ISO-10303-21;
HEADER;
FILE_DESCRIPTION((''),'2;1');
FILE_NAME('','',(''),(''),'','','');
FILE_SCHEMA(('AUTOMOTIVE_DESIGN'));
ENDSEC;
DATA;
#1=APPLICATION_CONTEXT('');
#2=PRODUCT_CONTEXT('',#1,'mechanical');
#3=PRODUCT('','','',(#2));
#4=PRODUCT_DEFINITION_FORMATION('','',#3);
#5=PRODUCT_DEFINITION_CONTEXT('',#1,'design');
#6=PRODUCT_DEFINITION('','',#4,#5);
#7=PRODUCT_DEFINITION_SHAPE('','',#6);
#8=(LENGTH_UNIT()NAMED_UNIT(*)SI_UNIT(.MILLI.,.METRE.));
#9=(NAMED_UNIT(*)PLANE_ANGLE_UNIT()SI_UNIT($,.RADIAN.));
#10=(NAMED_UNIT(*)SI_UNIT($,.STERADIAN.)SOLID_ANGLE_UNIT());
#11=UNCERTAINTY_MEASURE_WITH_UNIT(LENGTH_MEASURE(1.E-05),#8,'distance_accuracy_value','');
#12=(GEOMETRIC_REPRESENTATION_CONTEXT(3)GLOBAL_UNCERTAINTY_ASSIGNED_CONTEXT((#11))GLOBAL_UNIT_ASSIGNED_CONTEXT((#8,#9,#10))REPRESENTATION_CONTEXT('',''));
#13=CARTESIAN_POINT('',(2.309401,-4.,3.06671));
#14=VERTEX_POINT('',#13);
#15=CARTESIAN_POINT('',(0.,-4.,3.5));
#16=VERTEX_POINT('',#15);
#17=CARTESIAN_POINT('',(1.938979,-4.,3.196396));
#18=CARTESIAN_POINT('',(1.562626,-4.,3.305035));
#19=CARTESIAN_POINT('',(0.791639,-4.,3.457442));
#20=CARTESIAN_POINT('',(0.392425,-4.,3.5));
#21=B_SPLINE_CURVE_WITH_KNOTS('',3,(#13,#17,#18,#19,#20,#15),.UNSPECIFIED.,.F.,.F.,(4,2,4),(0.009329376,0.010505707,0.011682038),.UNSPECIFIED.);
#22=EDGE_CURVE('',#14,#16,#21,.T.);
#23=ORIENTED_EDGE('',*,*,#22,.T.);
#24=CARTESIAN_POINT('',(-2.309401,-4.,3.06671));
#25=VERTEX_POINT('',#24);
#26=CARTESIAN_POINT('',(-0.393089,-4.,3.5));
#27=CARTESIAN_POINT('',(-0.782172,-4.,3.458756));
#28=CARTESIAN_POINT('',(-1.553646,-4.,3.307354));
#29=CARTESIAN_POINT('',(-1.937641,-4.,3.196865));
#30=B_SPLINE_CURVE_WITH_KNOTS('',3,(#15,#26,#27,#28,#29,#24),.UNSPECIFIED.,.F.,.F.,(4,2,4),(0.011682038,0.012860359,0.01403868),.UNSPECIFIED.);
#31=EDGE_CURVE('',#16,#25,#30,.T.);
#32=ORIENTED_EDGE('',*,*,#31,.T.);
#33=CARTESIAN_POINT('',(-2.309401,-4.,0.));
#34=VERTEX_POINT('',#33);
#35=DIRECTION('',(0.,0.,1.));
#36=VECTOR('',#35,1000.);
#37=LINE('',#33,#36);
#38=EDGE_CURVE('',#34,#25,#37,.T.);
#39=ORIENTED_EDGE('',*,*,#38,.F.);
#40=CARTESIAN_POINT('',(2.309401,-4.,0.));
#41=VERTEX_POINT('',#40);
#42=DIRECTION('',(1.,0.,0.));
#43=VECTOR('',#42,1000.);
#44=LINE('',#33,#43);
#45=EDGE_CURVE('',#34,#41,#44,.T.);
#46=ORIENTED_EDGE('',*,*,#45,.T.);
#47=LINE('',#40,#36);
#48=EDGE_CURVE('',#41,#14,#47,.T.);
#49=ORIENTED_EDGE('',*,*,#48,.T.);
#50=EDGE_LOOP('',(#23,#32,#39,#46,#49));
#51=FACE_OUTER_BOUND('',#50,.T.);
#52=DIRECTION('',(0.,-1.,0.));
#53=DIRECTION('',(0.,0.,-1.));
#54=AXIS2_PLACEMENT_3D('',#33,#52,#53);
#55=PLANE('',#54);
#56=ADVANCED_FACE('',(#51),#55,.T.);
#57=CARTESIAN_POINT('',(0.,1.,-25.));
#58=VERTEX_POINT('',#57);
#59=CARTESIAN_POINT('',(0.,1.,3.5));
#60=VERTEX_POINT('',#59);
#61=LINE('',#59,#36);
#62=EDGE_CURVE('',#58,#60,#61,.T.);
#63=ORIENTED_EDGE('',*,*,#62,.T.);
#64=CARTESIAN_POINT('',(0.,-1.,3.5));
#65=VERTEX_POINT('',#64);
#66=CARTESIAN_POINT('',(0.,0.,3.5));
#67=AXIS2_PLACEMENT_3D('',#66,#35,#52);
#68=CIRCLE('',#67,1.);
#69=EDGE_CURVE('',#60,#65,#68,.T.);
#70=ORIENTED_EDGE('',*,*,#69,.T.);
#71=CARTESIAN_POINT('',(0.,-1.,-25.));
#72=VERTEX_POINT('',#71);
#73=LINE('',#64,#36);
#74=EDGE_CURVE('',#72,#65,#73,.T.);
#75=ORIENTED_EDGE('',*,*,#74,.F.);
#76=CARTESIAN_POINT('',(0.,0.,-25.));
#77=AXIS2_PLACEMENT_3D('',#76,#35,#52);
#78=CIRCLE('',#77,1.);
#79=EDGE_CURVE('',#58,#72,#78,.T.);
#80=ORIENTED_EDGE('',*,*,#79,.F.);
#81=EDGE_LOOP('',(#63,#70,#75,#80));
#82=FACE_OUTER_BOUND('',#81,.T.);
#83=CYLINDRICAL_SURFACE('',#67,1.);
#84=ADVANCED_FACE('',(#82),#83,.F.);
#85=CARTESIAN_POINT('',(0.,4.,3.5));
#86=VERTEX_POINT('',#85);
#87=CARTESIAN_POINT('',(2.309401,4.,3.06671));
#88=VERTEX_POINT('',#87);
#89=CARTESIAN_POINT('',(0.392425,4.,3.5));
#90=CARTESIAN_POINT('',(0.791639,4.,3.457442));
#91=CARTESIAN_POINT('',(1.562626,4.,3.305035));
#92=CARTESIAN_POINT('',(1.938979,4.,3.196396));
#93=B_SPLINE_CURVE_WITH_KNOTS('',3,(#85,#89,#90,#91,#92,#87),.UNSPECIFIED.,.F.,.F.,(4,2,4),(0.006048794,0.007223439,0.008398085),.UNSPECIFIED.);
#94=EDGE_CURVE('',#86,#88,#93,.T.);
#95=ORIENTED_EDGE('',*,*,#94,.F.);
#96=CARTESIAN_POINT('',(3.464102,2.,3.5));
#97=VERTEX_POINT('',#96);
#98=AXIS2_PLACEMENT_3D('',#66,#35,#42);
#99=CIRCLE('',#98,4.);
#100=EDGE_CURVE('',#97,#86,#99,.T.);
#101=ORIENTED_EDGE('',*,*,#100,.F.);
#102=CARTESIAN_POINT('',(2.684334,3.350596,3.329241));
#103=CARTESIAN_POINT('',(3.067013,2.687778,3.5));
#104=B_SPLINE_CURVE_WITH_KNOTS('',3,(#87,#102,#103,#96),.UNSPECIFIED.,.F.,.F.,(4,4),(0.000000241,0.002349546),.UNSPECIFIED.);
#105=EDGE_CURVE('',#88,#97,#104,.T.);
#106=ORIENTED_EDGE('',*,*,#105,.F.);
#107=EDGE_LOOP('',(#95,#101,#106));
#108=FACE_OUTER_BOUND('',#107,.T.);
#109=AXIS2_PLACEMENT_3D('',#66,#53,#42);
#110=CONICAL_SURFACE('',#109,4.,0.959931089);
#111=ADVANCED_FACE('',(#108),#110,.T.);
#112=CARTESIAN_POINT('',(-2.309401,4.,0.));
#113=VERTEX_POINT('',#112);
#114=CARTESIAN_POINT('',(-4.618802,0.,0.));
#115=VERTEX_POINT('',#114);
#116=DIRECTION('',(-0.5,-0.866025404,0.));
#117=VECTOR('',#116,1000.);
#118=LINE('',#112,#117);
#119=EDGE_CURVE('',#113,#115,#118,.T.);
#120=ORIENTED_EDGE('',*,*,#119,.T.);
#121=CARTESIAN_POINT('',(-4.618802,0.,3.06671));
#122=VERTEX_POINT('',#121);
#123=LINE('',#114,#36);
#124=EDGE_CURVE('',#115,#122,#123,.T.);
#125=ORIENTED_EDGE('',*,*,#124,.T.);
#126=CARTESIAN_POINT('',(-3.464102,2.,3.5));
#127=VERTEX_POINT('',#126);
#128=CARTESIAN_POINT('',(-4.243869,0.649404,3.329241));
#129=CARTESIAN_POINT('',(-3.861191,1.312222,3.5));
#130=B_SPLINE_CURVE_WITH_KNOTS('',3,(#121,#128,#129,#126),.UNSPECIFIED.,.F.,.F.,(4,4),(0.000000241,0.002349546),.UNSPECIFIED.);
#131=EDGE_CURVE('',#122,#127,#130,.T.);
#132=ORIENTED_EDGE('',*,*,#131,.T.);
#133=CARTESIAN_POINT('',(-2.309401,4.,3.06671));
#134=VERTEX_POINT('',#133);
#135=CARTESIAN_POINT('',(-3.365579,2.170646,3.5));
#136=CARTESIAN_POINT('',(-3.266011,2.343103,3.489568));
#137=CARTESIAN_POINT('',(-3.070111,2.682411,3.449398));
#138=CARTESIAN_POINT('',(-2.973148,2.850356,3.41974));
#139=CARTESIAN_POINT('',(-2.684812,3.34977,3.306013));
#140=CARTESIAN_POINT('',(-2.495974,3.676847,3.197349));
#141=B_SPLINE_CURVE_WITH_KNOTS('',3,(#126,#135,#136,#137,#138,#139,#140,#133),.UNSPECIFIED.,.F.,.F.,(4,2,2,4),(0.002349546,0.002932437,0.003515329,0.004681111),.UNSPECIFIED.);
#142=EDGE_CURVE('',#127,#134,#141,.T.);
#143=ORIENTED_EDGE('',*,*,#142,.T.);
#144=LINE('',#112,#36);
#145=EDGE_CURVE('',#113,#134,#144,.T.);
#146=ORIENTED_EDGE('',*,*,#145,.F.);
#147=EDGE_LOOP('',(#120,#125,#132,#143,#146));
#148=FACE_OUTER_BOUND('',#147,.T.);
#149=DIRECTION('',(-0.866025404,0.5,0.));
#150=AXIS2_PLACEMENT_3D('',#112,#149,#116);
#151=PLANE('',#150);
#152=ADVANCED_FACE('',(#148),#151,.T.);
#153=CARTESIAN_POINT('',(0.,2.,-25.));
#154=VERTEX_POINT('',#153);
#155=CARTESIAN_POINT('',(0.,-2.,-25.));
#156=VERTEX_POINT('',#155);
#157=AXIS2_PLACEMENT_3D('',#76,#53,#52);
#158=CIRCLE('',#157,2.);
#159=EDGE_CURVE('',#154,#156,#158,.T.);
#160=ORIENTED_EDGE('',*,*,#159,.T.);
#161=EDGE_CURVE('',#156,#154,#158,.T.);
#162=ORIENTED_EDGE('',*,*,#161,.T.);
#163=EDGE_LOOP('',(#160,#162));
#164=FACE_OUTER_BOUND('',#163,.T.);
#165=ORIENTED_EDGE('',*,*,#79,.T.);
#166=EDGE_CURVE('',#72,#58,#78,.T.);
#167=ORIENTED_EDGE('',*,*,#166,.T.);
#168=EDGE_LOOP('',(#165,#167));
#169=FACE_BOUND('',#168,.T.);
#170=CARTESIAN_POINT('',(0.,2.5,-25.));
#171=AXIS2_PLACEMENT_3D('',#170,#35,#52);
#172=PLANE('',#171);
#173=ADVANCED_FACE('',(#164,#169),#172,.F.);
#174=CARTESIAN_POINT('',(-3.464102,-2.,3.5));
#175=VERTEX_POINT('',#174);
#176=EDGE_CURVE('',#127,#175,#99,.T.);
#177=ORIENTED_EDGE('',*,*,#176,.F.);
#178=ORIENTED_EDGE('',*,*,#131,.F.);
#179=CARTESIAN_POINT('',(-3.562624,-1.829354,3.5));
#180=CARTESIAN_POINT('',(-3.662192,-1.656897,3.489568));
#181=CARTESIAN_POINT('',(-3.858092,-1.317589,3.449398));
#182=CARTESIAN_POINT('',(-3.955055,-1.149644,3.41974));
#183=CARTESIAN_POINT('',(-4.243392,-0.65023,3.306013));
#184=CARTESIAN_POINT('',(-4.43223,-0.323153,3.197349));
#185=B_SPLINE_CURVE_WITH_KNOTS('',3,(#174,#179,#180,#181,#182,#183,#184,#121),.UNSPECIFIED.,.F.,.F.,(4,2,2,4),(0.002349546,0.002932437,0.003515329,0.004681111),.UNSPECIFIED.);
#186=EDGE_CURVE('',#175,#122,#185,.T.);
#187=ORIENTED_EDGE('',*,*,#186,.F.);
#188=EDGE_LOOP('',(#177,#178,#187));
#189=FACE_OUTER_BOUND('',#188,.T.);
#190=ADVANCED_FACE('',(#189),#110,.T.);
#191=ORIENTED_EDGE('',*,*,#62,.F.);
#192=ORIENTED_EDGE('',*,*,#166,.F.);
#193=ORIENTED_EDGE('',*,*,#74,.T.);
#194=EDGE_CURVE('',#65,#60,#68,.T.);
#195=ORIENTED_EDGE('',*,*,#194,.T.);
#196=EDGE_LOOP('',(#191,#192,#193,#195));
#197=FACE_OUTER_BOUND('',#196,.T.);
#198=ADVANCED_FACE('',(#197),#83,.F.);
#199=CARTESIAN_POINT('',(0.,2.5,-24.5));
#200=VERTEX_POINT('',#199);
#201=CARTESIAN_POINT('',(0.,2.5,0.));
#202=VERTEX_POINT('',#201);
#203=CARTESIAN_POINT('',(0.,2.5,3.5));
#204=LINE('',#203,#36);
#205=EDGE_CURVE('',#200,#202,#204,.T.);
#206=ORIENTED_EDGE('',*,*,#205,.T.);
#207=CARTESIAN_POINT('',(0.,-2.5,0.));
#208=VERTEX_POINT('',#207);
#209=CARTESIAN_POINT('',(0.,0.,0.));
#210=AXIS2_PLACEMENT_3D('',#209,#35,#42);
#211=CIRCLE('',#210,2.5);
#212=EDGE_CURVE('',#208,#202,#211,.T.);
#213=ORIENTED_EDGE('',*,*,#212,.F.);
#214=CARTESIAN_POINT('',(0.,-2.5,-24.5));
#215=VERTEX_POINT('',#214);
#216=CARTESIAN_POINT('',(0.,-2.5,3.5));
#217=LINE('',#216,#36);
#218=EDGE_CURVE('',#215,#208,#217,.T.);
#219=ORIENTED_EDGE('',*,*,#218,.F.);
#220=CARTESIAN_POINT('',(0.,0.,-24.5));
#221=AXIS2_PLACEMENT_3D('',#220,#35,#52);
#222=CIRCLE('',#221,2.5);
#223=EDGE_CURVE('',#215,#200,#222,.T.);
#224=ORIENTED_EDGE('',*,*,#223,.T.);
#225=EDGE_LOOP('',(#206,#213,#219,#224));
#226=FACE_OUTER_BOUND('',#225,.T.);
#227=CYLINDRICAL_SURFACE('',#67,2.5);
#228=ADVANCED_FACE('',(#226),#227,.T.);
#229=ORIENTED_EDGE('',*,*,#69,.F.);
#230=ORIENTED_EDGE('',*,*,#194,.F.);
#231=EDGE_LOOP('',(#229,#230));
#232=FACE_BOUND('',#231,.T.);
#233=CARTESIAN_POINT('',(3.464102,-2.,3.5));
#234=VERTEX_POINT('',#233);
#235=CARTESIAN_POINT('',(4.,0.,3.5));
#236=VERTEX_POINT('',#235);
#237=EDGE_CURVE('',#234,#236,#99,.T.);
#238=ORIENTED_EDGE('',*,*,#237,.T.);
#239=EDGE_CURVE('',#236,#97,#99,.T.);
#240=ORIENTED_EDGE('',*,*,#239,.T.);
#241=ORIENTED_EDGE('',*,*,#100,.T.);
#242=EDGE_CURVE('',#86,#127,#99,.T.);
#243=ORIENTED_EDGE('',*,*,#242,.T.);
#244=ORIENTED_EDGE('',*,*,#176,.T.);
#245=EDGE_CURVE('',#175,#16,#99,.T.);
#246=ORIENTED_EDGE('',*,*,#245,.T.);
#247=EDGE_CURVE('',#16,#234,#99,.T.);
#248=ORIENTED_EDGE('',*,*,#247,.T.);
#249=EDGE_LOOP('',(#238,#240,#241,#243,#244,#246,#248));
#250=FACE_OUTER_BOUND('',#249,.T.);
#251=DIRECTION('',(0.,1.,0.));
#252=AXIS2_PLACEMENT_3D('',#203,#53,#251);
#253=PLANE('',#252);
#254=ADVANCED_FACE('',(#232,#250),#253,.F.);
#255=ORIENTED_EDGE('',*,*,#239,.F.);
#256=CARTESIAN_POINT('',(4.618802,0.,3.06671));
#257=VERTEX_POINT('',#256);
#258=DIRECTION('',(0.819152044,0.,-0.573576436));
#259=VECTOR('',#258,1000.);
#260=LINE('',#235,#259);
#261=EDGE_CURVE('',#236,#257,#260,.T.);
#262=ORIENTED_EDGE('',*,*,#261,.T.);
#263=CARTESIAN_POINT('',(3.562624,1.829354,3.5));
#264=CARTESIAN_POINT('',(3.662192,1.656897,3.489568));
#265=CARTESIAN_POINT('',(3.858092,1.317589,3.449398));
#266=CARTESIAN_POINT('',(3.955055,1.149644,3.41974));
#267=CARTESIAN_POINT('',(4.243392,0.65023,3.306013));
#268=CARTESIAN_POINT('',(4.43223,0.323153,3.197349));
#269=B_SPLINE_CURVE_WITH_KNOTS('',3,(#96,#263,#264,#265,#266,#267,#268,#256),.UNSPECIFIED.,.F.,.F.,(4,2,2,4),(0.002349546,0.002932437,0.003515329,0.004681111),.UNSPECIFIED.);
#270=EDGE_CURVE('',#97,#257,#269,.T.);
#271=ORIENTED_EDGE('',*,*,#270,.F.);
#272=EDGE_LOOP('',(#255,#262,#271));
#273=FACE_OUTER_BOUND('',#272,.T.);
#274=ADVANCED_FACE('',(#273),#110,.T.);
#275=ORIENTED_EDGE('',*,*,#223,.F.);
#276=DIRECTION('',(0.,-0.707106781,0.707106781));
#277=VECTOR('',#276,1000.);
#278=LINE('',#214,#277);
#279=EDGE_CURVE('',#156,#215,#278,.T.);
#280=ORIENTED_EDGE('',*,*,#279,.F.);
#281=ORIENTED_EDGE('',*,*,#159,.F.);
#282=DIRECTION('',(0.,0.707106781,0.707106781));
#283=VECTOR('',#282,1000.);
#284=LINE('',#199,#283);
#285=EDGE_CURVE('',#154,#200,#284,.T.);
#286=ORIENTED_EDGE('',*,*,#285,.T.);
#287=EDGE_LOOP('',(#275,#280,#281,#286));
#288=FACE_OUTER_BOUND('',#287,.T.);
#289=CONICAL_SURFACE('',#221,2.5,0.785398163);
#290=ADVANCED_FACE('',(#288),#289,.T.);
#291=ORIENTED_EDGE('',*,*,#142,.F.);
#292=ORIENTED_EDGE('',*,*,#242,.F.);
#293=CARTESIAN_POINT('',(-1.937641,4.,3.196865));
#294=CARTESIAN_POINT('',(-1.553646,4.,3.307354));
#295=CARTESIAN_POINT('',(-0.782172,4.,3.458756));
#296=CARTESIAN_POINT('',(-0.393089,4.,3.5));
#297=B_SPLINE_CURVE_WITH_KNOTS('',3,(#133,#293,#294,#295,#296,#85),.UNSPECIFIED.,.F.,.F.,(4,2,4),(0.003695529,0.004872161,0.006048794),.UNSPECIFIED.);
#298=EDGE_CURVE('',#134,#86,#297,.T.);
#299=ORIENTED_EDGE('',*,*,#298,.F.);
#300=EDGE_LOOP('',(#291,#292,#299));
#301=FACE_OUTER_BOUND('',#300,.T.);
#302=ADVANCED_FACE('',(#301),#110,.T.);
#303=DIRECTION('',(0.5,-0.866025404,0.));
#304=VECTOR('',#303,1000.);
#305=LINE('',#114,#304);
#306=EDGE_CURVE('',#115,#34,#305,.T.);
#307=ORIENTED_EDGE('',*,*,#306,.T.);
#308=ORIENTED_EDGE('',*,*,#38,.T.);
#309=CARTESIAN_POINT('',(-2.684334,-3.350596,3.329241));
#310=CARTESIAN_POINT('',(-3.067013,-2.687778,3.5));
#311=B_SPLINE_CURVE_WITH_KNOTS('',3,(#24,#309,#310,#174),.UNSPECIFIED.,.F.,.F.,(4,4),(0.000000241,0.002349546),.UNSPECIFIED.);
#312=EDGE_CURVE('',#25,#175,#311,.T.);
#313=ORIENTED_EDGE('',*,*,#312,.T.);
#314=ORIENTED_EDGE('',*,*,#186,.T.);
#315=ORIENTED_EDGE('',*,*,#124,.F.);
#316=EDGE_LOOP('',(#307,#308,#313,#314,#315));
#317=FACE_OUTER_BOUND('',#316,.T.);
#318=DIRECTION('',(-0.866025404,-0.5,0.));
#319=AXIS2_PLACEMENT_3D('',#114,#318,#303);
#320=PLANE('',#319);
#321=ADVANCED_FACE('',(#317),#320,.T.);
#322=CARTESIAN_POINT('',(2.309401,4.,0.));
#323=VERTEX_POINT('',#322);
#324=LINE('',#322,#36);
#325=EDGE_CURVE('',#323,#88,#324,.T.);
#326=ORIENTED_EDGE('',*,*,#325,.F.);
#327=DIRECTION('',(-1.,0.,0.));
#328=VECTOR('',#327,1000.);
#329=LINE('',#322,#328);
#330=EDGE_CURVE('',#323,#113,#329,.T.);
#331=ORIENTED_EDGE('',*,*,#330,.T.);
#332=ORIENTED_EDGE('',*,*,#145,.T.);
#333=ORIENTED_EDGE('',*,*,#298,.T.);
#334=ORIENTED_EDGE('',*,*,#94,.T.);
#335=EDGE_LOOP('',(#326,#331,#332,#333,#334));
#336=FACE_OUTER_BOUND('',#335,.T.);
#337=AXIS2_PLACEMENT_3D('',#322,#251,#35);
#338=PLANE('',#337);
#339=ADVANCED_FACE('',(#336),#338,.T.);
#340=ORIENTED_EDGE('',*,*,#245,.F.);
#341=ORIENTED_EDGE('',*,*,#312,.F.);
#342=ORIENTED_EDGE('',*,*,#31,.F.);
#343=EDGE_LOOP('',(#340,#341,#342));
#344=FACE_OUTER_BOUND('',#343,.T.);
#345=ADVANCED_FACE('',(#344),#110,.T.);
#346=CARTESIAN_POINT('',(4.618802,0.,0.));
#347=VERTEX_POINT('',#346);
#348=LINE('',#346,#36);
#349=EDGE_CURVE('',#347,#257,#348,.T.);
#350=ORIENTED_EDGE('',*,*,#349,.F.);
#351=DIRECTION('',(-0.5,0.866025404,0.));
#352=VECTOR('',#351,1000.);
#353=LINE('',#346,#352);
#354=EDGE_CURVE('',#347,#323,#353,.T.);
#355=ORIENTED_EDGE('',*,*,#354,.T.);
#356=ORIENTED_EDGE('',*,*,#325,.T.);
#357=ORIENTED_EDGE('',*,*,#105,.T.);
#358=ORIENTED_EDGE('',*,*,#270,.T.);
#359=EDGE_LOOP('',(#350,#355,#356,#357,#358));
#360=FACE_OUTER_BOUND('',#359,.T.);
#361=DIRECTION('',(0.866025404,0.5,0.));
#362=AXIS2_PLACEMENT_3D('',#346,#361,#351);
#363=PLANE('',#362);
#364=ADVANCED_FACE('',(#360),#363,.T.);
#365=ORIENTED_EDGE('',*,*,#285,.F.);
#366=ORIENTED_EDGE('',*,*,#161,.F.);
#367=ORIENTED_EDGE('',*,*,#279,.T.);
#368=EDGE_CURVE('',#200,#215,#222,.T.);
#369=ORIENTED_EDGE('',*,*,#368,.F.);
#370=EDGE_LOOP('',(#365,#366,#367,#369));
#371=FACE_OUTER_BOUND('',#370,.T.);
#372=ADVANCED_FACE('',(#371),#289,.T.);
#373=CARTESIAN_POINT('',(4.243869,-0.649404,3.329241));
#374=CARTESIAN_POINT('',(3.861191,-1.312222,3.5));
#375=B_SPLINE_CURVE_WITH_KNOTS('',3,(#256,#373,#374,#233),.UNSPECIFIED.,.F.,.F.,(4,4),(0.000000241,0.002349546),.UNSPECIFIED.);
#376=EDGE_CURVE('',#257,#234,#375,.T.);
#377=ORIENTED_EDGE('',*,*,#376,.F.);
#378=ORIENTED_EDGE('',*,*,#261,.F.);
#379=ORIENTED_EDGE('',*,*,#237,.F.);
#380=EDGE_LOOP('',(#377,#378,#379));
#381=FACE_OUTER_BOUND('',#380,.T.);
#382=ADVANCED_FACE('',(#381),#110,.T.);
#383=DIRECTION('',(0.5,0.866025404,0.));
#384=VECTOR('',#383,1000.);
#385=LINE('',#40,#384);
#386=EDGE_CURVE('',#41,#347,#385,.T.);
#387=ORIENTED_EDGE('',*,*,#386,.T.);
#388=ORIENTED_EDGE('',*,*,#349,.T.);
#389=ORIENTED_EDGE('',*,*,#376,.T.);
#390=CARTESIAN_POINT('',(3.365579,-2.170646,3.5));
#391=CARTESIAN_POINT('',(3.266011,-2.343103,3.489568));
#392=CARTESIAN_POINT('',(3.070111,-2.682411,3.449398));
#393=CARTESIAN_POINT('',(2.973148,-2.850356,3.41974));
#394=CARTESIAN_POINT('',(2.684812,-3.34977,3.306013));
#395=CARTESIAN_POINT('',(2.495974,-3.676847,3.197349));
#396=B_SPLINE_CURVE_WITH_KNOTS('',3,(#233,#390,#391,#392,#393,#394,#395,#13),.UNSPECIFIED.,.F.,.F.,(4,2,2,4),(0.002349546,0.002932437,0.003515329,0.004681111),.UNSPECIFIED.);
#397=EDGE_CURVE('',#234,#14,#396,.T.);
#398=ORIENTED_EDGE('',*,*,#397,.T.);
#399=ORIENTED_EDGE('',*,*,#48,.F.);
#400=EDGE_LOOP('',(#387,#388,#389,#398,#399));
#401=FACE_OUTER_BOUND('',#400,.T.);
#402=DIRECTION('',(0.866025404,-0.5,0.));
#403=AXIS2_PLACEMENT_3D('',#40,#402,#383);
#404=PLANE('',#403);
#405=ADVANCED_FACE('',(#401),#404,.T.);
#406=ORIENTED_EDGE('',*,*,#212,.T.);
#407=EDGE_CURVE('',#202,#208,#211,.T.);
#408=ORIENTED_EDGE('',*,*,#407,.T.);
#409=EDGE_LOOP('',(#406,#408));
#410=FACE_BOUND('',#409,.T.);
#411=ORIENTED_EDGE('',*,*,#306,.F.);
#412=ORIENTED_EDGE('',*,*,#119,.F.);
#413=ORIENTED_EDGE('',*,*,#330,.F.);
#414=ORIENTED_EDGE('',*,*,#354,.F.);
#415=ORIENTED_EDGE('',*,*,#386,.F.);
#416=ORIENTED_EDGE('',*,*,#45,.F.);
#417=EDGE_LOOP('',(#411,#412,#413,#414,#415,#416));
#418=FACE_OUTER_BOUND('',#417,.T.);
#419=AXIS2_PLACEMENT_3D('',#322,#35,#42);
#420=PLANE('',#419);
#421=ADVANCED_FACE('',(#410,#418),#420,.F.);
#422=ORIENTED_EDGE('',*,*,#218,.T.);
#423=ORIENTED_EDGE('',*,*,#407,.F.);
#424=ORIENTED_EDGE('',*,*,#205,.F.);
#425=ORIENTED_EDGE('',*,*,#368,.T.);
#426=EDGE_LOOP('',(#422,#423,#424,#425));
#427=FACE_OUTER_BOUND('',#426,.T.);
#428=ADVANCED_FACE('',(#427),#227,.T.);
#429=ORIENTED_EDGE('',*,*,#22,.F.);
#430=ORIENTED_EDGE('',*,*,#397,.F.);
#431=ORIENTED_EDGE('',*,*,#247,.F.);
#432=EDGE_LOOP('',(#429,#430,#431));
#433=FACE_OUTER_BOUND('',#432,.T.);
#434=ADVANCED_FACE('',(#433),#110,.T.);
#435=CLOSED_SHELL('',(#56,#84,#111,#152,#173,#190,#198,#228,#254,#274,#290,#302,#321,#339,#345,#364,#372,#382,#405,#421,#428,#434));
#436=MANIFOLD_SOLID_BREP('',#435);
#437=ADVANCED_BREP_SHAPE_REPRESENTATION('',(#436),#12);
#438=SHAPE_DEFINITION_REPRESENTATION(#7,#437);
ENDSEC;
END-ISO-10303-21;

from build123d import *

# Parameters (mm, degrees)
BOSS_EXTRUDE1_START = -3.5
SKETCH4_R           = 1
BOSS_EXTRUDE1_DEPTH = 3.5
SKETCH5_R           = 5.237604307
SKETCH5_R_2         = 4
CUT_EXTRUDE1_DEPTH  = 1
CUT_EXTRUDE1_DRAFT  = -55
CHAMFER1_SIZE       = 0.5


with BuildPart() as part:
    # Sketch3 → Revolve1 (revolve)
    with BuildSketch(Plane(origin=(0, 0, 0), x_dir=(0, 0, -1), z_dir=(1, 0, 0)), mode=Mode.PRIVATE) as revolve1_sk:
        Polygon((0, 2.5), (-3.5, 2.5), (-3.5, 1), (25, 1), (25, 2.5), align=None)
    revolve(revolve1_sk.sketch.rotate(Axis((0, 0, 3.5), (0, 0, -1)), 180), axis=Axis((0, 0, 3.5), (0, 0, -1)))

    # Sketch4 → Boss-Extrude1 (add)
    with BuildSketch(Plane.XY.offset(3.5).offset(BOSS_EXTRUDE1_START)):
        Polygon((2.309401077, 4), (-2.309401077, 4), (-4.618802154, 0), (-2.309401077, -4), (2.309401077, -4), (4.618802154, 0), align=None)
        with Locations(Location((0, 0, 0), (0, 0, 270))):
            Circle(SKETCH4_R, mode=Mode.SUBTRACT)
    extrude(amount=BOSS_EXTRUDE1_DEPTH)


with BuildPart() as cut_extrude1_tool:
    # Sketch5 → Cut-Extrude1 (with draft: the straight prism first)
    with BuildSketch(Plane.XY.offset(3.5)):
        Circle(SKETCH5_R)
        Circle(SKETCH5_R_2, mode=Mode.SUBTRACT)
    extrude(amount=-CUT_EXTRUDE1_DEPTH)
    # Cut-Extrude1: the draft: its side faces are tilted about the plane it starts from
    cut_extrude1_sides = [cut_extrude1_tool.faces().sort_by_distance(p)[0] for p in [
        (-5.237604307, 0, 3),
        (-4, 0, 3),
    ]]
    draft(cut_extrude1_sides, Plane.XY.offset(3.5), CUT_EXTRUDE1_DRAFT)


with BuildPart() as part_1:
    add(part.part)

    # Cut-Extrude1: cut by cut_extrude1_tool
    add(cut_extrude1_tool.part, mode=Mode.SUBTRACT)

    # Chamfer1
    chamfer1_edges = [part_1.edges().sort_by_distance(p)[0] for p in [
        (0, 2.5, -25),
    ]]
    chamfer(chamfer1_edges, length=CHAMFER1_SIZE)


solid = part_1.part
